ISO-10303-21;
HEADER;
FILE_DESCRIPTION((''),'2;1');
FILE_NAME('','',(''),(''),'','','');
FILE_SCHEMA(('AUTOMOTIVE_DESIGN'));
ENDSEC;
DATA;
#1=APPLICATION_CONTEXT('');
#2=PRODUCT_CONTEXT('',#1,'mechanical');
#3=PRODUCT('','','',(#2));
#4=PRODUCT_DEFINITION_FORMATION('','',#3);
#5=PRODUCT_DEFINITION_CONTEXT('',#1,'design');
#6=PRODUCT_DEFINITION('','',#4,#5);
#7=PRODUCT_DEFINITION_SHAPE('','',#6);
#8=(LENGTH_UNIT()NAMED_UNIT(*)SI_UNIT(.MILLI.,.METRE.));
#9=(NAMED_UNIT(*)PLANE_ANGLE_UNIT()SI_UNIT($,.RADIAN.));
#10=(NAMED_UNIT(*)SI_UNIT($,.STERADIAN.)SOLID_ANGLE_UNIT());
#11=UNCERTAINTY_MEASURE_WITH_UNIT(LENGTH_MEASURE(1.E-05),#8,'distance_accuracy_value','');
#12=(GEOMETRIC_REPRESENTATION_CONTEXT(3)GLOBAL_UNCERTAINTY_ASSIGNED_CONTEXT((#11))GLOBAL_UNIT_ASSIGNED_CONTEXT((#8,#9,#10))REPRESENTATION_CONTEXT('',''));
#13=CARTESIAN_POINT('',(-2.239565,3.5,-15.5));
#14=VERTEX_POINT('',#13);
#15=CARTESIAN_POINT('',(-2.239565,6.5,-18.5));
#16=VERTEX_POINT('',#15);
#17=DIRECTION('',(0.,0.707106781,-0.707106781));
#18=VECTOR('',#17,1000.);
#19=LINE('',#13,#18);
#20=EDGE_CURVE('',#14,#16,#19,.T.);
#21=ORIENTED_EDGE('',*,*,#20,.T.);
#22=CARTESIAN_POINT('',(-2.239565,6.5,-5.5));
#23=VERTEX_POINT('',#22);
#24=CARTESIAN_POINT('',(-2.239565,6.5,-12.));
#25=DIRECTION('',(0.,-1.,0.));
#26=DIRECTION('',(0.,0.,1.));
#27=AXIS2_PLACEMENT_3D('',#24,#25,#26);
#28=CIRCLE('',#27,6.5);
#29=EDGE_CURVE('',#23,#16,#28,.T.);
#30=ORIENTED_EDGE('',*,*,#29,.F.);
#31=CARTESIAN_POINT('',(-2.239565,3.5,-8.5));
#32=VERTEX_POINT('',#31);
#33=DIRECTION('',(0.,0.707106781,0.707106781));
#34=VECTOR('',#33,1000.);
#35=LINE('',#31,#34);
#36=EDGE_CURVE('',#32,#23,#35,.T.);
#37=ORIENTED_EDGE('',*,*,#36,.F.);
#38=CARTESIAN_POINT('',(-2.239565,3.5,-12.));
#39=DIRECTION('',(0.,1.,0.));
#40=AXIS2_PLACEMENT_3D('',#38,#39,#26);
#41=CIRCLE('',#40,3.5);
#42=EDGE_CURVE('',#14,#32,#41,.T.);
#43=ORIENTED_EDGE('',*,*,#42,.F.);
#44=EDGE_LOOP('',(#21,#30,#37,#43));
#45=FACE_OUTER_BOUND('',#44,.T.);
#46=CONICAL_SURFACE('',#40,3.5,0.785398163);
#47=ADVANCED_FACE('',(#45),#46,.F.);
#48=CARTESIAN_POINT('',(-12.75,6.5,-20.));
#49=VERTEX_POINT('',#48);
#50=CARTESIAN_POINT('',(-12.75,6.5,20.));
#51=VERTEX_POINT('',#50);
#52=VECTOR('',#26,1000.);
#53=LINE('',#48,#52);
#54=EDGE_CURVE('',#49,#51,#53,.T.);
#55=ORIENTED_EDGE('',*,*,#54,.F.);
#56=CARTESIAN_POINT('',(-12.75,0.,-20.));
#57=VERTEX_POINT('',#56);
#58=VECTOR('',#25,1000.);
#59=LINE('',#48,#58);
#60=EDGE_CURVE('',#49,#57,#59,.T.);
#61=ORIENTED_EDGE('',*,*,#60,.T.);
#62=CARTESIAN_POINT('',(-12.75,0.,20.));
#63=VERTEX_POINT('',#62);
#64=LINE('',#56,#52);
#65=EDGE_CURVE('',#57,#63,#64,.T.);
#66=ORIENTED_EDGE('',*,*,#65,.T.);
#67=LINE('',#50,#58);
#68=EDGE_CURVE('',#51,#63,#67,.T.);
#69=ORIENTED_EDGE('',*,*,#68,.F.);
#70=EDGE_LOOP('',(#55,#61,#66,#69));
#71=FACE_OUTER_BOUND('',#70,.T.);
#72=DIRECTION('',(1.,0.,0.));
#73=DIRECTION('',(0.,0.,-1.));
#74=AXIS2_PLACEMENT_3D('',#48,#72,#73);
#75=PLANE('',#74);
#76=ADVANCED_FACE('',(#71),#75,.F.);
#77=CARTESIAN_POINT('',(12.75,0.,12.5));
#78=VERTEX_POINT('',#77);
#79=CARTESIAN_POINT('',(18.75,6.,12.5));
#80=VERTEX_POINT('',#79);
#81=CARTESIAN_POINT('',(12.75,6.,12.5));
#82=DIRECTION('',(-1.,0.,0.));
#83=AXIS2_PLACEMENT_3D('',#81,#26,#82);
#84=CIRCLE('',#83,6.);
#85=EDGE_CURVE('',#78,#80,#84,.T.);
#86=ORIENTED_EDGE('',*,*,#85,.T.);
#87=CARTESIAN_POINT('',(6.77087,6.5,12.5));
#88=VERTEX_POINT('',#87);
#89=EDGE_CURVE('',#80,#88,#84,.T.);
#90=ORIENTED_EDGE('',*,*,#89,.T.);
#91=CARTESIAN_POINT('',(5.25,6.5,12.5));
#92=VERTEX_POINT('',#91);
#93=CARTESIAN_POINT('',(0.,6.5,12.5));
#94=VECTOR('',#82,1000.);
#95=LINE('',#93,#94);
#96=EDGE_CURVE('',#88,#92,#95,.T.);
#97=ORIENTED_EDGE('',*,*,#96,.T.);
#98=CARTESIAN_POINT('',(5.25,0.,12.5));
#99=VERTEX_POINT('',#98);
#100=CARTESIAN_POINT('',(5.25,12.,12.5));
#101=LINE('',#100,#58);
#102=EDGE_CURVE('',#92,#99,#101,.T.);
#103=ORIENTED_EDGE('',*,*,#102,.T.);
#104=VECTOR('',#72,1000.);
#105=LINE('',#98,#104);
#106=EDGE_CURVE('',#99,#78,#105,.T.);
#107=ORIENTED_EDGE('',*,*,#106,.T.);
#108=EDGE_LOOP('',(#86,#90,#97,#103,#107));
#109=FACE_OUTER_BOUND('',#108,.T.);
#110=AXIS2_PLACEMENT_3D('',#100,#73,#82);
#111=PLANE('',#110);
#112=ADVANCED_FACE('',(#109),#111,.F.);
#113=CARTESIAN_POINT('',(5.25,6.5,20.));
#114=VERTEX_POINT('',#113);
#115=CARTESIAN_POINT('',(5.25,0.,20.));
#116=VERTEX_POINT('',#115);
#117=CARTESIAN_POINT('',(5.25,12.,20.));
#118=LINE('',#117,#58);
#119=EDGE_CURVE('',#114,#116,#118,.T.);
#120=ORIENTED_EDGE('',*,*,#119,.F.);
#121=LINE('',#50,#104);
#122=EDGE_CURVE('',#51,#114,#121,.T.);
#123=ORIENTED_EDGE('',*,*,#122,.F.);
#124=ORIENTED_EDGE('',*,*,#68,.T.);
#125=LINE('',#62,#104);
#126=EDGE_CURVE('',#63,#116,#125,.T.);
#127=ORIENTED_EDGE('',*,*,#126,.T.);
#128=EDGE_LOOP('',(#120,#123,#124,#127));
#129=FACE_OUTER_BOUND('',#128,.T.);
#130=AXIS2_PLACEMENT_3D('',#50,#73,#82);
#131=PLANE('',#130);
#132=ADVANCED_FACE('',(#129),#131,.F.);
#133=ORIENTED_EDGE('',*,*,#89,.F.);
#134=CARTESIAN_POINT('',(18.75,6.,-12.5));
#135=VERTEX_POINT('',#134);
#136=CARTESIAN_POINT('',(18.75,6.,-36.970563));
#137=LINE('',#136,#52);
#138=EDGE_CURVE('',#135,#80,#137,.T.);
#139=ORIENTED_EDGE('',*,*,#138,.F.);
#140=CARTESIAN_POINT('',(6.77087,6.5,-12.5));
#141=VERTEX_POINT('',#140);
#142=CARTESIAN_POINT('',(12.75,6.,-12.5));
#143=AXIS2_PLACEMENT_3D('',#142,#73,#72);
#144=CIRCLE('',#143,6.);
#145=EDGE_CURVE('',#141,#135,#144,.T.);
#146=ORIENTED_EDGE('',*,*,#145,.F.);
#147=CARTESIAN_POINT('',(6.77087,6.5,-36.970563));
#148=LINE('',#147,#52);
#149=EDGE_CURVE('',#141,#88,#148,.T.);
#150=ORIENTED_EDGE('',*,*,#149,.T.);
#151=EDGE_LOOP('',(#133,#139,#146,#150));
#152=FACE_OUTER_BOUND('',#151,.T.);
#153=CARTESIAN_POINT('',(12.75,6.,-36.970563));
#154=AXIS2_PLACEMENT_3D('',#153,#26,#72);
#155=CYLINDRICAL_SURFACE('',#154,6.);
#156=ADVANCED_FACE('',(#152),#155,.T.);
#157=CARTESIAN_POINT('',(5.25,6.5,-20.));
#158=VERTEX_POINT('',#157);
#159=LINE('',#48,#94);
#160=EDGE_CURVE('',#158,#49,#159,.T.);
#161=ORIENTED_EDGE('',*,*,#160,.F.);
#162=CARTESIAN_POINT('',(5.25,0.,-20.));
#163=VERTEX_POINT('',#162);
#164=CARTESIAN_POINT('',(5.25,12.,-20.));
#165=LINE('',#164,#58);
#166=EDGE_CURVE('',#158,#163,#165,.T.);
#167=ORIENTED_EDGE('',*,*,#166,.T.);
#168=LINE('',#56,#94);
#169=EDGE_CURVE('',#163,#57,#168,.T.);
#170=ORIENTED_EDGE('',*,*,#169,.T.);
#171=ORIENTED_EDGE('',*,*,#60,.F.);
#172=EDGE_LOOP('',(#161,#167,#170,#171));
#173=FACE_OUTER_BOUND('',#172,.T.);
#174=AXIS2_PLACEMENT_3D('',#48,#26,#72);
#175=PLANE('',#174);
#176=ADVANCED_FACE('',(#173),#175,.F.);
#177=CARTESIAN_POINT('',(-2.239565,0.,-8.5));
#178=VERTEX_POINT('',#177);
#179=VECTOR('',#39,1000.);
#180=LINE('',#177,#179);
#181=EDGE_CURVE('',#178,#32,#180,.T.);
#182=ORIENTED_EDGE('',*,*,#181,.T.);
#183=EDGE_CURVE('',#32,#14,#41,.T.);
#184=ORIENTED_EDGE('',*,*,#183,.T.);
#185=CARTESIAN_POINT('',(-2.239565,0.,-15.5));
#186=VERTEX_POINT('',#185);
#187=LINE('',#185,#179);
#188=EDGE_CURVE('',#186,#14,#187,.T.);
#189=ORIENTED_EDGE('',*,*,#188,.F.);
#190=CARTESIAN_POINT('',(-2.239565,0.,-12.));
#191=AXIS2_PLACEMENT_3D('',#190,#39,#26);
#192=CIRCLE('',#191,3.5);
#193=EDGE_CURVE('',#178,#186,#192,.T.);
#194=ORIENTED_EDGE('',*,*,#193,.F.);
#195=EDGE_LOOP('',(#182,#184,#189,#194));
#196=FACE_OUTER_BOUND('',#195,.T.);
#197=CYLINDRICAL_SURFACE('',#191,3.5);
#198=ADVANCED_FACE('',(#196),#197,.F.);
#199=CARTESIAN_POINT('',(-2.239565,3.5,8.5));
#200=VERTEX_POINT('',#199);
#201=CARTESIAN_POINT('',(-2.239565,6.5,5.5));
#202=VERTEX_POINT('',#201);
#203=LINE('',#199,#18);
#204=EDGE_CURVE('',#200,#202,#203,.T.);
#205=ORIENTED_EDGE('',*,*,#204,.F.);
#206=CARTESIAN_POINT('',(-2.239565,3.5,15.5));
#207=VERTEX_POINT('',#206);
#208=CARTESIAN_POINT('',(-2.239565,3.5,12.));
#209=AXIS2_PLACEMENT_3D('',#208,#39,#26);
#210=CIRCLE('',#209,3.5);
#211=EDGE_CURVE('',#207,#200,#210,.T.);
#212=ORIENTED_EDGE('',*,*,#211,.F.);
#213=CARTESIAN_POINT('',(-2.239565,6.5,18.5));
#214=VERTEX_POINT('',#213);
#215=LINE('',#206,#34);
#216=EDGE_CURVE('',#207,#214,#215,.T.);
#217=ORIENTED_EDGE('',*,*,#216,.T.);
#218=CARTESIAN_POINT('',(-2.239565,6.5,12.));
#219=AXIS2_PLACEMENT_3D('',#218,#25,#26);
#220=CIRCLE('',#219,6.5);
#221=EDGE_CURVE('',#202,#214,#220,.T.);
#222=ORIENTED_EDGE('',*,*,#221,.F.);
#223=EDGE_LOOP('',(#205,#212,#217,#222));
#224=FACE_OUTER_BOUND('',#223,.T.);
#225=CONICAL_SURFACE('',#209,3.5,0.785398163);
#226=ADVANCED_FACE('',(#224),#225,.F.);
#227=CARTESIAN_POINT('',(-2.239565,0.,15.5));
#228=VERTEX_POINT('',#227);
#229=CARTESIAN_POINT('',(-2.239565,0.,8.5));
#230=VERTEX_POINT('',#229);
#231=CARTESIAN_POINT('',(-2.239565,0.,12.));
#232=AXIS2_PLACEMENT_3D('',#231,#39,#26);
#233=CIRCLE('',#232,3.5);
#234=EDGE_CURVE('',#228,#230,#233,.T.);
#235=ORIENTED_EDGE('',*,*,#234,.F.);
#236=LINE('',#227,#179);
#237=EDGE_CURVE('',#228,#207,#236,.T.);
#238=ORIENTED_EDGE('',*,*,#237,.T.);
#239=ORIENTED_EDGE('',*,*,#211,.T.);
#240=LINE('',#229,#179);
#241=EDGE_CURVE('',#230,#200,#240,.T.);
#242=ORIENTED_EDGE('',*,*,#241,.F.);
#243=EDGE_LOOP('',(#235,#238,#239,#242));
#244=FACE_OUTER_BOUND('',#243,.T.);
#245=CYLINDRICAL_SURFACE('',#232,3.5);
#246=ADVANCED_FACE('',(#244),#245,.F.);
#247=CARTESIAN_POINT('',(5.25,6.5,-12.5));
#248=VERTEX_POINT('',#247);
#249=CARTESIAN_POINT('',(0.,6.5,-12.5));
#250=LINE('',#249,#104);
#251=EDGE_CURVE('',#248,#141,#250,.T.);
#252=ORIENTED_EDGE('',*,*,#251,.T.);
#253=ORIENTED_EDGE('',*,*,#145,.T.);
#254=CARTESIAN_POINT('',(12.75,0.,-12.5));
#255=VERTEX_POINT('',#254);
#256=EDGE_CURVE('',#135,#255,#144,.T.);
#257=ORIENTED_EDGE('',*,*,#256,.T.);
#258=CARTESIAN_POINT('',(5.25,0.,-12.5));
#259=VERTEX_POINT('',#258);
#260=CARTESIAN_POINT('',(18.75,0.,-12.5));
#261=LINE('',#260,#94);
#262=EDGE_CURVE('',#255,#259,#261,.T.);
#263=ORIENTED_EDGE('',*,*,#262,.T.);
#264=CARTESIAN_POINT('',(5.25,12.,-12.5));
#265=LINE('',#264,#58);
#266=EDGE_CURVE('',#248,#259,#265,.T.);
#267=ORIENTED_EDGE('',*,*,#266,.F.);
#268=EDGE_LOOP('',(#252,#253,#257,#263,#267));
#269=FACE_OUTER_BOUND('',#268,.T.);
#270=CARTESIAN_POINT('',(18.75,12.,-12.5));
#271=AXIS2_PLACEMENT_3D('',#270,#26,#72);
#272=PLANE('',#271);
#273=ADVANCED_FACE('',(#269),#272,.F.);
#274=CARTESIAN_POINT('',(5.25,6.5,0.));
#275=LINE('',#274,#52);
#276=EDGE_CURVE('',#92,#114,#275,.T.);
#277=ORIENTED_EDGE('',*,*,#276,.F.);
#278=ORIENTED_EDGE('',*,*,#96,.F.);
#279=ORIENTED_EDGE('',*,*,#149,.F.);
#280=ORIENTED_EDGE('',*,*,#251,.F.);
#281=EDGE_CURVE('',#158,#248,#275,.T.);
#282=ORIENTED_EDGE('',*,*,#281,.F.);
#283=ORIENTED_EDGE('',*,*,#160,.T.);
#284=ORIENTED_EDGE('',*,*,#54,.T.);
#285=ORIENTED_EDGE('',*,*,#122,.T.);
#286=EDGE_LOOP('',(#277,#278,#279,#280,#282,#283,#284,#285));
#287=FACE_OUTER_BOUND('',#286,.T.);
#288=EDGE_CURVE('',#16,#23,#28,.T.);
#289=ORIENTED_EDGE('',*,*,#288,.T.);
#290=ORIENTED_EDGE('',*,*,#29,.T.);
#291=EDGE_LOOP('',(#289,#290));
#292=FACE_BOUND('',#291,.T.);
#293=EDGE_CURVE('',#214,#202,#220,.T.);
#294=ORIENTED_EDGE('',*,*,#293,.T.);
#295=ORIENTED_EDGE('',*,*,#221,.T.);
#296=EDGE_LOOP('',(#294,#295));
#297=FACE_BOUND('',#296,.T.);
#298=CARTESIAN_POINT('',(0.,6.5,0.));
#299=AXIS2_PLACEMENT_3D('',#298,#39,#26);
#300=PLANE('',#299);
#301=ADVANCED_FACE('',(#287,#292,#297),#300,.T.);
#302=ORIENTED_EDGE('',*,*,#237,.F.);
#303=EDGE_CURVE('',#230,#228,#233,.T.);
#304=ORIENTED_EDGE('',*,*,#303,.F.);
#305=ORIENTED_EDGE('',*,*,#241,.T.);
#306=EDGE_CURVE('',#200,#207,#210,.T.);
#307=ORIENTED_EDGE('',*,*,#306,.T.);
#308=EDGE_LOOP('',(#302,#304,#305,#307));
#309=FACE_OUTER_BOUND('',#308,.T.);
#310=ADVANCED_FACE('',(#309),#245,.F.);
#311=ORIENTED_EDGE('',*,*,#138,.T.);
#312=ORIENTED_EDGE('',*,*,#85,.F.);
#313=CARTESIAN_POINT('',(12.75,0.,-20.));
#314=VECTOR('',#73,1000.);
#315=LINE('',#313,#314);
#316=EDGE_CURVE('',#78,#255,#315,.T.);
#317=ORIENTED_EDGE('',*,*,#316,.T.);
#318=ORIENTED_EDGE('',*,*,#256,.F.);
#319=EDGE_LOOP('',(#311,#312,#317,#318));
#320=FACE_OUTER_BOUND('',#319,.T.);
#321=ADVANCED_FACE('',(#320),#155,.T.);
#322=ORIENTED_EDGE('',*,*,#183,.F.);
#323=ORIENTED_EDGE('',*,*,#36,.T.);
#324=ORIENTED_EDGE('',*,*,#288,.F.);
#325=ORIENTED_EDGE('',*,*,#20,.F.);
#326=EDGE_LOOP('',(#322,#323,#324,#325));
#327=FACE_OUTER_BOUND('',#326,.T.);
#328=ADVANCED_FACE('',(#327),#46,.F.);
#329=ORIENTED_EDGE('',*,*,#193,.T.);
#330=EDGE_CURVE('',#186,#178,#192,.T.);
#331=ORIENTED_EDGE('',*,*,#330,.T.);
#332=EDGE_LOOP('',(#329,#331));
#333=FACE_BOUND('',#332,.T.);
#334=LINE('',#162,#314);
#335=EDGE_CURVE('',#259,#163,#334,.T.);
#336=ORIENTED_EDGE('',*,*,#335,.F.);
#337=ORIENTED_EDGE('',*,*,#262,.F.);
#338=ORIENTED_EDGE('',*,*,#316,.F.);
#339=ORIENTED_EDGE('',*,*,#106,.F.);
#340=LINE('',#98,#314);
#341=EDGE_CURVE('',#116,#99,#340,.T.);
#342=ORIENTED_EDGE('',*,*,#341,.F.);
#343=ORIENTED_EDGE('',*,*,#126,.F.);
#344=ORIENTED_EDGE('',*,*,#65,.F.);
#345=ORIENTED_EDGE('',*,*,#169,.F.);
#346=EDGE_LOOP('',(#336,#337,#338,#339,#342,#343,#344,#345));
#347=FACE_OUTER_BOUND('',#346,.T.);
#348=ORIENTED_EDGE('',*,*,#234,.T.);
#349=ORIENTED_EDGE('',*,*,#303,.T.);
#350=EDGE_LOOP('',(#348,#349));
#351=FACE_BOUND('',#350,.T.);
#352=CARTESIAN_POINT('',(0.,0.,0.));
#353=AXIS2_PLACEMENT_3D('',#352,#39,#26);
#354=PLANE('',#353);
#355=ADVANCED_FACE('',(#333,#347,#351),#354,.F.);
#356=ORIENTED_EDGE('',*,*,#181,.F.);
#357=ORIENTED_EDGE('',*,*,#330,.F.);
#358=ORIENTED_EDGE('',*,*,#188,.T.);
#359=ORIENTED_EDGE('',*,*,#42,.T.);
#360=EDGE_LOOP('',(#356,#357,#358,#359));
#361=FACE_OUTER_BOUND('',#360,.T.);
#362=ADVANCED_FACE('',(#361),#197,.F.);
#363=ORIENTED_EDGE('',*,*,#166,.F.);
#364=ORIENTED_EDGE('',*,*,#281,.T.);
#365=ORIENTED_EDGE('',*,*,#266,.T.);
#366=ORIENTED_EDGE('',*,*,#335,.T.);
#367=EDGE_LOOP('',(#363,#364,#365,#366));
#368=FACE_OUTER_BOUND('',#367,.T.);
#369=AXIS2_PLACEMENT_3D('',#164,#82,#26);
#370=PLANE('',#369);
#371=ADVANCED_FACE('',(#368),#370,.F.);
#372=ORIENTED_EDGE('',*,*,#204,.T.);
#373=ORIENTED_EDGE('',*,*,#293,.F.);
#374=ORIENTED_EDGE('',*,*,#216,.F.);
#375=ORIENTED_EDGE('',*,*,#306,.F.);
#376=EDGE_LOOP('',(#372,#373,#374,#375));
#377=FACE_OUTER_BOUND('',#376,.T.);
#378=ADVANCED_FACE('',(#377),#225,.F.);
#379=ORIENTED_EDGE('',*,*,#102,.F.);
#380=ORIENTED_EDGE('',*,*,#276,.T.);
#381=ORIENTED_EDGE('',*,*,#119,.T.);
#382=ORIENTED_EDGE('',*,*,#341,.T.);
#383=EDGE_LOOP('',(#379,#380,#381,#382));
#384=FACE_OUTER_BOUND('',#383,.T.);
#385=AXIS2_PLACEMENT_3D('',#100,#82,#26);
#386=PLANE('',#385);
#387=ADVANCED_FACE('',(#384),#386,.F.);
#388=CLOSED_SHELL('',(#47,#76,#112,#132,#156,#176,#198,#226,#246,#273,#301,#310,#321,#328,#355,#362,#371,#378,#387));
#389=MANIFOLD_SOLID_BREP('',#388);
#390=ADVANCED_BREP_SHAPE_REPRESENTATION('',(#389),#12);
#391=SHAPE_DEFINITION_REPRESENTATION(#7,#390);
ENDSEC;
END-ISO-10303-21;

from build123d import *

# Parameters (mm, degrees)
SKETCH_1_W          = 25.5
SKETCH_1_H          = 40
EXTRUDE_1_DEPTH     = 6.5
SKETCH_2_R          = 6
EXTRUDE_2_DEPTH     = 40
SKETCH_3_W          = 13.5
SKETCH_3_H          = 7.5
CUT_EXTRUDE_1_DEPTH = 30.925950277
SKETCH_5_R          = 3.5
CUT_EXTRUDE_2_DEPTH = 29.174678348
CHAMFER_1_SIZE      = 3


with BuildPart() as part:
    # 草图1 → 凸台-拉伸1 (new body)
    with BuildSketch(Plane(origin=(0, 0, 0), x_dir=(1, 0, 0), z_dir=(0, 1, 0))):
        Rectangle(SKETCH_1_W, SKETCH_1_H)
    extrude(amount=EXTRUDE_1_DEPTH)

    # 草图2 → 凸台-拉伸2 (add)
    with BuildSketch(Plane.XY.offset(20)):
        with Locations((12.75, 6)):
            Circle(SKETCH_2_R)
    extrude(amount=-EXTRUDE_2_DEPTH)

    # 草图3 → 切除-拉伸1 (cut, through all)
    with BuildSketch(Plane.XZ):
        with Locations((12, 16.25)):
            Rectangle(SKETCH_3_W, SKETCH_3_H)
        with Locations((12, -16.25)):
            Rectangle(SKETCH_3_W, SKETCH_3_H)
    extrude(amount=-CUT_EXTRUDE_1_DEPTH, mode=Mode.SUBTRACT)

    # 草图5 → 切除-拉伸2 (cut, through all)
    with BuildSketch(Plane(origin=(0, 6.5, 0), x_dir=(1, 0, 0), z_dir=(0, 1, 0))):
        with Locations(Location((-2.239565186, 12, 0), (0, 0, 270))):
            Circle(SKETCH_5_R)
        with Locations(Location((-2.239565186, -12, 0), (0, 0, 270))):
            Circle(SKETCH_5_R)
    extrude(amount=-CUT_EXTRUDE_2_DEPTH, mode=Mode.SUBTRACT)

    # 倒角1
    chamfer_1_edges = [part.edges().sort_by_distance(p)[0] for p in [
        (-2.239565186, 6.5, -15.5),
        (-2.239565186, 6.5, 8.5),
    ]]
    chamfer(chamfer_1_edges, length=CHAMFER_1_SIZE)


solid = part.part
